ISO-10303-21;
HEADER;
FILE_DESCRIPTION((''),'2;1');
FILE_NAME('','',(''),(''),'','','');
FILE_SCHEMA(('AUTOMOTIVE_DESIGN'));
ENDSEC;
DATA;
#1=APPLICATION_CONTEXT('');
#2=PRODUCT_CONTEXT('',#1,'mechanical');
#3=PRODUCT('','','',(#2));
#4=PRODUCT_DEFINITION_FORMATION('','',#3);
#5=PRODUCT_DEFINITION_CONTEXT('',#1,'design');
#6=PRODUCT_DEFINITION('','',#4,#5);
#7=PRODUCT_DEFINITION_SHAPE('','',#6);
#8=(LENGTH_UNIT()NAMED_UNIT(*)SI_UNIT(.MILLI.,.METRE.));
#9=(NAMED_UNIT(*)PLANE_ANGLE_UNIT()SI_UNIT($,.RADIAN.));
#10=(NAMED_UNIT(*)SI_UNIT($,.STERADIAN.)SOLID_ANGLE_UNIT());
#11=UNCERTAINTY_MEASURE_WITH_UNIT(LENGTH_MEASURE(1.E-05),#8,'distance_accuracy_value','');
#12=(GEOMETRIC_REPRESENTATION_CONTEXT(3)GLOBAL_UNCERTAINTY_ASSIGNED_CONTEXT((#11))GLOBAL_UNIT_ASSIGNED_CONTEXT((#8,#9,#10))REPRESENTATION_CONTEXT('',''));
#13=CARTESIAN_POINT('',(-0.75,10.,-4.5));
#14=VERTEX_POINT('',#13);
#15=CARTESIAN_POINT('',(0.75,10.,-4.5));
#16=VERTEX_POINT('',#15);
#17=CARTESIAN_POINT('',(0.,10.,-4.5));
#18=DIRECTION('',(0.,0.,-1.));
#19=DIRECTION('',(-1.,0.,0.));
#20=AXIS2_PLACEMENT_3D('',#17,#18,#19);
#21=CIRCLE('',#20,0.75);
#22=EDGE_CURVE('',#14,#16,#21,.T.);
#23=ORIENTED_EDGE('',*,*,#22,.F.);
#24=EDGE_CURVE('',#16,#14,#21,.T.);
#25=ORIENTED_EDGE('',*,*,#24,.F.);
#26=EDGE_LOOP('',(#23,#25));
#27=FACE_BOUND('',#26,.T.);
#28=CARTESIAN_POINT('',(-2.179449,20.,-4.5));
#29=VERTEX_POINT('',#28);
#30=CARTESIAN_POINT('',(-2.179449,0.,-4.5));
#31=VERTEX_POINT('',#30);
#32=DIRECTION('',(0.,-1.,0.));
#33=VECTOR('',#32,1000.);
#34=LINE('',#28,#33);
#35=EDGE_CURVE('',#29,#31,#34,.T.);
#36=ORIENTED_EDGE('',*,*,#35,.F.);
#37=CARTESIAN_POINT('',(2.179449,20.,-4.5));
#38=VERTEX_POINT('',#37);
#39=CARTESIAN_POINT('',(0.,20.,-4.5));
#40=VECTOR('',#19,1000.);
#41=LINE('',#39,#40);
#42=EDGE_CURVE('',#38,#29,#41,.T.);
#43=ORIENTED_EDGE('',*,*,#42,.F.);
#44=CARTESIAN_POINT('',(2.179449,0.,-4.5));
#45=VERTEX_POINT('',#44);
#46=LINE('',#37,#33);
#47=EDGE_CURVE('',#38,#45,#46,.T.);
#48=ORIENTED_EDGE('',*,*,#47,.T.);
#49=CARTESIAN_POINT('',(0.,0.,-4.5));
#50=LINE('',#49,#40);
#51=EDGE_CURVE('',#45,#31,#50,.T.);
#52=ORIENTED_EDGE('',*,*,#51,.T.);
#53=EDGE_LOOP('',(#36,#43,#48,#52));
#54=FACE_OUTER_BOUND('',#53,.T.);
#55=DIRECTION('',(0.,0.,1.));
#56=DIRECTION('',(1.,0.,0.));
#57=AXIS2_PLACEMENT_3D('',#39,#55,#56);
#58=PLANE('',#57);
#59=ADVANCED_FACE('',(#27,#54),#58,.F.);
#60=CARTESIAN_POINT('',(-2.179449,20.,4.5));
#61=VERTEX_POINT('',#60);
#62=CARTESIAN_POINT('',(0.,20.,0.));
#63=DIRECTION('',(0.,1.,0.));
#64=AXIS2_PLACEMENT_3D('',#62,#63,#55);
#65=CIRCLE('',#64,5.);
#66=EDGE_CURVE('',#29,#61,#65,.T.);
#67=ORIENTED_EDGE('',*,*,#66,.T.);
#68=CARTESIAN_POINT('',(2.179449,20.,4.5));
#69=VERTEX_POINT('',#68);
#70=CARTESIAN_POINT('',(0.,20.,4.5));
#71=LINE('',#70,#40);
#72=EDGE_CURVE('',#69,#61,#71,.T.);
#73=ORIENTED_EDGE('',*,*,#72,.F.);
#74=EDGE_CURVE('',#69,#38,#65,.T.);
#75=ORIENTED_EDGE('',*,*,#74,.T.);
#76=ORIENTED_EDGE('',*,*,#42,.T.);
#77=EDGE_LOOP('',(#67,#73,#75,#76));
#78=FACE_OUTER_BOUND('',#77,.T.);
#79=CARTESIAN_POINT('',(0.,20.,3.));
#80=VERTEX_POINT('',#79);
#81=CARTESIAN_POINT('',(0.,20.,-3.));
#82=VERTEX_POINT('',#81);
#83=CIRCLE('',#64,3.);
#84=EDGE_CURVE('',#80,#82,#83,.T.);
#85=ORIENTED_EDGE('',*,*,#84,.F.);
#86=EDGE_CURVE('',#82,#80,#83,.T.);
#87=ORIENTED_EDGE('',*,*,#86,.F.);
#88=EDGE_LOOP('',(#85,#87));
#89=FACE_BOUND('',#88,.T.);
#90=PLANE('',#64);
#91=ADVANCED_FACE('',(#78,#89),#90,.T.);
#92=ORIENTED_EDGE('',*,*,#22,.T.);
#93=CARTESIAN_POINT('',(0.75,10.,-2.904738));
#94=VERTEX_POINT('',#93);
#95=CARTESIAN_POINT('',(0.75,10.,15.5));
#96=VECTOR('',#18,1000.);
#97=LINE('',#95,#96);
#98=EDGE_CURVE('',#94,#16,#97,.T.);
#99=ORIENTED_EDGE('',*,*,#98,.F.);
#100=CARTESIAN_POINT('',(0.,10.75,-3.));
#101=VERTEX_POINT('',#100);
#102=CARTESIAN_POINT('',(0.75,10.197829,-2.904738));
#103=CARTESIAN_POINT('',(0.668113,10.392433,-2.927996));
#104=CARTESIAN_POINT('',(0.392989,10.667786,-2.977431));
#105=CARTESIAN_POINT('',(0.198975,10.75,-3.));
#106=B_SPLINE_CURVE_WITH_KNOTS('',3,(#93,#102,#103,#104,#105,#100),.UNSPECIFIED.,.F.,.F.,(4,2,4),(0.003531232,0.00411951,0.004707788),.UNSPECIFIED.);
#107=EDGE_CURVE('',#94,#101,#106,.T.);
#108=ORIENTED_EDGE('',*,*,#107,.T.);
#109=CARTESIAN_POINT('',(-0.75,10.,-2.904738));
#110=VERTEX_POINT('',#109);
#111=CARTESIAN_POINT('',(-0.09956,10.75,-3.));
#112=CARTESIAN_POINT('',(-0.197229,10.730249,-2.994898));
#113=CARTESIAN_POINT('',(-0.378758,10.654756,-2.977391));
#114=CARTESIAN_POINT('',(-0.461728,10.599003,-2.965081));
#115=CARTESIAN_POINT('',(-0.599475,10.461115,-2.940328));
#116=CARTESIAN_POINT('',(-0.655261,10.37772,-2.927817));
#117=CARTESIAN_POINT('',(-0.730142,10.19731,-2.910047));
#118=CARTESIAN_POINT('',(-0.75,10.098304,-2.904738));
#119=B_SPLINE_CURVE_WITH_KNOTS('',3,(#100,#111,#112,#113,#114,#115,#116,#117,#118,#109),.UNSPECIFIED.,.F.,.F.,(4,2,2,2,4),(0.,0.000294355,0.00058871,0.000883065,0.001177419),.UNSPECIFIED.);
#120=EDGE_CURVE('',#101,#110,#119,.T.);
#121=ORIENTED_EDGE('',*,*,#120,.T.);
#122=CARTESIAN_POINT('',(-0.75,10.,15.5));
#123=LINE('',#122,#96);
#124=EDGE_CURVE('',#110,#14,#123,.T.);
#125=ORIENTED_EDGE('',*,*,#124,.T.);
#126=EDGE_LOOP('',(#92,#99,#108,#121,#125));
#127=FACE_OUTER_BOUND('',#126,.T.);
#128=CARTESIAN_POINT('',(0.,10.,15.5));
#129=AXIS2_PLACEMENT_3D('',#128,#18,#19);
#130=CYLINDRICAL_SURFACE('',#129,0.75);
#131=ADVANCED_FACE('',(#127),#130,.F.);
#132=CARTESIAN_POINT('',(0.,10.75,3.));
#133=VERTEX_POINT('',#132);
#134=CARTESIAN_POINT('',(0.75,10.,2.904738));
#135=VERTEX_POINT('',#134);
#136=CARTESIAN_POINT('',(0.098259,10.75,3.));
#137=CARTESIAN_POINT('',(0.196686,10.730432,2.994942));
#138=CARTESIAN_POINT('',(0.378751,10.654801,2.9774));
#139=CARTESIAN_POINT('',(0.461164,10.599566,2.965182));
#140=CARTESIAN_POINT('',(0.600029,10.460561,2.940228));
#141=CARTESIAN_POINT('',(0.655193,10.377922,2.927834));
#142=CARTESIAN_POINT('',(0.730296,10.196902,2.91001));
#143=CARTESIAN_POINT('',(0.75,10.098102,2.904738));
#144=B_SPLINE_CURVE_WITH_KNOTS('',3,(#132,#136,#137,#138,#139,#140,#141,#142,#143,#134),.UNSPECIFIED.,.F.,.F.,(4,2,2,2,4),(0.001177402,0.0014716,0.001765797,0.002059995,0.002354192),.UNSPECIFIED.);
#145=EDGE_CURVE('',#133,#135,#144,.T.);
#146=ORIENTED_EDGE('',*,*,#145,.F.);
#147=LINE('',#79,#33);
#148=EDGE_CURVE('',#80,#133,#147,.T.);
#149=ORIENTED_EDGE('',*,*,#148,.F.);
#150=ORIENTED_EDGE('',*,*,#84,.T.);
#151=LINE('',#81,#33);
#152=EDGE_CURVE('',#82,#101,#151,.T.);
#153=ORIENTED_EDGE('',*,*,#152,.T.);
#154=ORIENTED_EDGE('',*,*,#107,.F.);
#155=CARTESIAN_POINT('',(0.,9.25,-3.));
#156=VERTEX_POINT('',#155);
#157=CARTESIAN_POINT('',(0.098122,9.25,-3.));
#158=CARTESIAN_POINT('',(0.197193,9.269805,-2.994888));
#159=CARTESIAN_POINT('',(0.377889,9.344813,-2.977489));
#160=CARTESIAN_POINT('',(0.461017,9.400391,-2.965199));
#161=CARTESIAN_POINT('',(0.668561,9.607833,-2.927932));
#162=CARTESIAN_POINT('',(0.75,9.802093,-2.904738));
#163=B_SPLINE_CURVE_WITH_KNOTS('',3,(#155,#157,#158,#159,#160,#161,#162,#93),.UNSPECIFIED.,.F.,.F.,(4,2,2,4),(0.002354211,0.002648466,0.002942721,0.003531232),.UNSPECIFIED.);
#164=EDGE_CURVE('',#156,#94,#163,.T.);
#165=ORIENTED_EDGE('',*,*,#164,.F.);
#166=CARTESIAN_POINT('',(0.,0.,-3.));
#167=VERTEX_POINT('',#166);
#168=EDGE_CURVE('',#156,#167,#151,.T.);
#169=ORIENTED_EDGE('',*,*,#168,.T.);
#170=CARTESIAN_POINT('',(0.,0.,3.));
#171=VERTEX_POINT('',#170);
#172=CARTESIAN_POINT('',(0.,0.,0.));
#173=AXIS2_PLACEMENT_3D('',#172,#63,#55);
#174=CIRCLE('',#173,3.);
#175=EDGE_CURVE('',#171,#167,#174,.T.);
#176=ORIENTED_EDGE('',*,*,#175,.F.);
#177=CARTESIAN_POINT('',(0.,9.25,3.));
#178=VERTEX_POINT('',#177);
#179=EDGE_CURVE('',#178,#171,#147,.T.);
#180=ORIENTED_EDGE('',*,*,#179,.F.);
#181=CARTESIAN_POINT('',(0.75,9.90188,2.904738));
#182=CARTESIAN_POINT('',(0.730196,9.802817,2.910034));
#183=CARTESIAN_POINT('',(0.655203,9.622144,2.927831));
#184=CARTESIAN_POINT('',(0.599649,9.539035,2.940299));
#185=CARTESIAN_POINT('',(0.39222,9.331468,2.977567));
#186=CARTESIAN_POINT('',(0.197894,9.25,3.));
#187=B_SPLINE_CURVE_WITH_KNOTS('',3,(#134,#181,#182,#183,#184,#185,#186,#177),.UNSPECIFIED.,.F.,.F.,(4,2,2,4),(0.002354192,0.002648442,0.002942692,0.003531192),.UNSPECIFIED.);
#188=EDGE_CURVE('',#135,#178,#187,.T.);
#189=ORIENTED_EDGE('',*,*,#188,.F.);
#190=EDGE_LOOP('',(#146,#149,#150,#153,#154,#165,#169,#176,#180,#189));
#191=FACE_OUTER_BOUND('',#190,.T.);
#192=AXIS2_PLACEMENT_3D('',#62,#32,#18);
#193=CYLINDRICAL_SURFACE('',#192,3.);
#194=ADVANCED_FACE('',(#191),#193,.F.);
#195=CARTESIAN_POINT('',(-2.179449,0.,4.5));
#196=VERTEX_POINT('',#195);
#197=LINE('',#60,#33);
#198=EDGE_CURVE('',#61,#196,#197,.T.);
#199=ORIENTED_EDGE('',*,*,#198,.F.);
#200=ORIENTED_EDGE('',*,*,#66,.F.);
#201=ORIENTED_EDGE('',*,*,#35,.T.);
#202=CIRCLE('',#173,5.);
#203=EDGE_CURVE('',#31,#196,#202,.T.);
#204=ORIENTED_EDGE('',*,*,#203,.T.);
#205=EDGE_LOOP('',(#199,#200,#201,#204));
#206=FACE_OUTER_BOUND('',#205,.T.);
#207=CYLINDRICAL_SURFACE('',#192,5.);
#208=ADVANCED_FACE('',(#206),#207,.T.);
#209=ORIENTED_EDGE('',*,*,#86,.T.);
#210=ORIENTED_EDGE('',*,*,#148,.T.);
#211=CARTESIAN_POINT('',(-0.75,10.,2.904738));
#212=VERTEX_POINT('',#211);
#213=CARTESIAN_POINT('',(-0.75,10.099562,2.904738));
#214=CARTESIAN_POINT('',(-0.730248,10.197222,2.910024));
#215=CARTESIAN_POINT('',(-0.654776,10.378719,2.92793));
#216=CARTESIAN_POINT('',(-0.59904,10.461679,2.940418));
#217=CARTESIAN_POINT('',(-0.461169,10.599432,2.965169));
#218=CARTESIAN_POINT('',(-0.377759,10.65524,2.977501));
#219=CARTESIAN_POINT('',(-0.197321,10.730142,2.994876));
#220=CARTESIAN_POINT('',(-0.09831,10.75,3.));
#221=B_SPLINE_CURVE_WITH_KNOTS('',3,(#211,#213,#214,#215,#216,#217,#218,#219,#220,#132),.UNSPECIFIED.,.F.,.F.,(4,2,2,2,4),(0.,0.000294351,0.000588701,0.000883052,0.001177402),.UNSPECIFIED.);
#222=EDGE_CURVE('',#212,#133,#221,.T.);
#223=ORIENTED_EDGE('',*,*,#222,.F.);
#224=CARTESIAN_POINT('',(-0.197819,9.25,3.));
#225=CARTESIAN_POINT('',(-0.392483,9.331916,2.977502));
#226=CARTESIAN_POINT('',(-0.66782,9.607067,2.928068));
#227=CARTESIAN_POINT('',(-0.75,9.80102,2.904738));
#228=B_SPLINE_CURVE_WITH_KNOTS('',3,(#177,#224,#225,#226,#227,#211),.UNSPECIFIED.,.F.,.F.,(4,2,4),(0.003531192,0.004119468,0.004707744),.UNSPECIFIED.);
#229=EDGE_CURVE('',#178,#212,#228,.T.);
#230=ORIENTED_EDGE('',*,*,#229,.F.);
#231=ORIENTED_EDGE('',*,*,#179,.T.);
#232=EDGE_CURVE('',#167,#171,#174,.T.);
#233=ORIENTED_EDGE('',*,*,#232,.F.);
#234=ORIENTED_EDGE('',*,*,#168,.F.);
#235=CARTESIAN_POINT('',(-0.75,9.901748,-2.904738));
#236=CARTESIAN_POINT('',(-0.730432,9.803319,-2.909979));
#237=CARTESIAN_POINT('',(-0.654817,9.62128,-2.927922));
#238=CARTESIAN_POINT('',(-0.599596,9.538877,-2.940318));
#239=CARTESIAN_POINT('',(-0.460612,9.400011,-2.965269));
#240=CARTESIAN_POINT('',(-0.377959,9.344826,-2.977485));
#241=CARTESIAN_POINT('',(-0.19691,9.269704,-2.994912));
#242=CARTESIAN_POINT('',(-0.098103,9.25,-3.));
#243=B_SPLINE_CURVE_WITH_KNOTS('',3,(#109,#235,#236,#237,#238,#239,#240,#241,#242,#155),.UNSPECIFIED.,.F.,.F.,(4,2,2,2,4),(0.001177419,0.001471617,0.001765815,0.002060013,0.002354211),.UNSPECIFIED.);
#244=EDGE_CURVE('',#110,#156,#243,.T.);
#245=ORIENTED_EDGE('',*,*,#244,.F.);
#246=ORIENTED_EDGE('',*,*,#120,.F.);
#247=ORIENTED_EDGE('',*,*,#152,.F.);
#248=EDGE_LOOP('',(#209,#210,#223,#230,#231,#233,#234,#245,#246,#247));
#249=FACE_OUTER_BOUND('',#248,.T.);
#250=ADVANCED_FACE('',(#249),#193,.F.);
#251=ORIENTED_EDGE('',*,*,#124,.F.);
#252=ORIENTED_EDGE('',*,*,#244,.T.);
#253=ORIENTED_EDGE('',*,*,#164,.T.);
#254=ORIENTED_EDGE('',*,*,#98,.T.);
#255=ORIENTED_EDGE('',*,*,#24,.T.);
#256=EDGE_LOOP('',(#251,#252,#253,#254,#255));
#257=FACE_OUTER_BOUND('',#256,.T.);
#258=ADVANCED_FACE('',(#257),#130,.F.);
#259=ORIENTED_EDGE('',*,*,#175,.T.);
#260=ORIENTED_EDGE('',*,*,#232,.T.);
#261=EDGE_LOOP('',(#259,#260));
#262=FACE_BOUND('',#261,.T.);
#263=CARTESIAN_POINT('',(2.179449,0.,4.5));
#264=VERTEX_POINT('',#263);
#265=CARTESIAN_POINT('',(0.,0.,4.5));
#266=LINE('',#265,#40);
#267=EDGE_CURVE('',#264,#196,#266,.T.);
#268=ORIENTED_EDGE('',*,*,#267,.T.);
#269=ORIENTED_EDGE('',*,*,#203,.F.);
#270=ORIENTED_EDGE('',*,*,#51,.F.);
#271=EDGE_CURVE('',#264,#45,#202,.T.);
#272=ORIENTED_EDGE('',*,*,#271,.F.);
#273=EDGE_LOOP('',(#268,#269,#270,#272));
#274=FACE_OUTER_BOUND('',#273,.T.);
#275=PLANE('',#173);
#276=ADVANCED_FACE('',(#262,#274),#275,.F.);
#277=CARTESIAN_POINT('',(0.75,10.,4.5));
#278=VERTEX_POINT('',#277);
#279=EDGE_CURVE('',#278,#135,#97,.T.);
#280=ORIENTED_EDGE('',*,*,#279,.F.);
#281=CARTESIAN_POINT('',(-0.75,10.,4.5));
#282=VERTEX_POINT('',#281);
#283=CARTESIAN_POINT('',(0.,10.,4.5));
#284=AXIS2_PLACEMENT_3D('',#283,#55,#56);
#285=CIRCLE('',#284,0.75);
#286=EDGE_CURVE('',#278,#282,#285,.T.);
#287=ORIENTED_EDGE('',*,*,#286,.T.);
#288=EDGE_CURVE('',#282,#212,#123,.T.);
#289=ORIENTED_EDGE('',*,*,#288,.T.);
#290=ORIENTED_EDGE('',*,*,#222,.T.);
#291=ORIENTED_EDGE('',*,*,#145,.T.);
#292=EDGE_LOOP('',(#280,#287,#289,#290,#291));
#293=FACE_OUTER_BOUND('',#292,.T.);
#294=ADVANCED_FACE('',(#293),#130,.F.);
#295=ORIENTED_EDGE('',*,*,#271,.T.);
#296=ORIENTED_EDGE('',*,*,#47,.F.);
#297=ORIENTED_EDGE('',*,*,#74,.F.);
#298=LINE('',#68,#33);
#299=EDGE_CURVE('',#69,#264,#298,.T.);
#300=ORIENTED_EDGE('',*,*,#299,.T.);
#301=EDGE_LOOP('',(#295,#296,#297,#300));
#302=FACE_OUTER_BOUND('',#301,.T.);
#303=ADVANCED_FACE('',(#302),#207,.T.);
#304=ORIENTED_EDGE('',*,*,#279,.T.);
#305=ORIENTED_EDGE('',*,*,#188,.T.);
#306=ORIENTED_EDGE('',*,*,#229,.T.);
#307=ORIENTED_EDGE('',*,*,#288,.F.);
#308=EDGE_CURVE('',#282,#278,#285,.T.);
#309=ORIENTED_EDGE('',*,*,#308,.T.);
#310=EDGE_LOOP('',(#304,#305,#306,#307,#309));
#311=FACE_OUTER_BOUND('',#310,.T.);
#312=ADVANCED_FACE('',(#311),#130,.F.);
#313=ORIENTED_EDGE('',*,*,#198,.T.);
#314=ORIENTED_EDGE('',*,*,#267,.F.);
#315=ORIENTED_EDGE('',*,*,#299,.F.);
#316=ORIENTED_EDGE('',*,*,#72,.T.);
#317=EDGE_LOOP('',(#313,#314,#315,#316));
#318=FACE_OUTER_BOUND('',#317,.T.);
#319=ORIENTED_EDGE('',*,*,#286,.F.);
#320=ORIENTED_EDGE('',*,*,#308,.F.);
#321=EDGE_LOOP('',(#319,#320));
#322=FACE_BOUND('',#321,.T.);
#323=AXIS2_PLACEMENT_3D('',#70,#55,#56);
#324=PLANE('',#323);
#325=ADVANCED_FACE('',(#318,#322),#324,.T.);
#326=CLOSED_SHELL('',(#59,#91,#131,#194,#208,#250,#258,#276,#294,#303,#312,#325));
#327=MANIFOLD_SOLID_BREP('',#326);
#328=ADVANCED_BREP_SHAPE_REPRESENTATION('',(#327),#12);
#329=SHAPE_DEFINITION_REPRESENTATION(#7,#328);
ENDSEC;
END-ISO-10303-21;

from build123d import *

# Parameters (mm, degrees)
SKETCH1_R           = 3
BOSS_EXTRUDE1_DEPTH = 20
SKETCH2_R           = 0.75
CUT_EXTRUDE1_DEPTH  = 20


with BuildPart() as part:
    # Sketch1 → Boss-Extrude1 (new body)
    with BuildSketch(Plane(origin=(0, 0, 0), x_dir=(1, 0, 0), z_dir=(0, 1, 0))):
        with BuildLine():
            Line((2.179449472, -4.5), (-2.179449472, -4.5))
            ThreePointArc((-2.179449472, -4.5), (-5, 0), (-2.179449472, 4.5))
            Line((-2.179449472, 4.5), (2.179449472, 4.5))
            ThreePointArc((2.179449472, 4.5), (5, 0), (2.179449472, -4.5))
        make_face()
        with Locations(Location((0, 0, 0), (0, 0, 270))):
            Circle(SKETCH1_R, mode=Mode.SUBTRACT)
    extrude(amount=BOSS_EXTRUDE1_DEPTH)

    # Sketch2 → Cut-Extrude1 (cut)
    with BuildSketch(Plane(origin=(0, 0, -4.5), x_dir=(-1, 0, 0), z_dir=(0, 0, -1))):
        with Locations((0, 10)):
            Circle(SKETCH2_R)
    extrude(amount=-CUT_EXTRUDE1_DEPTH, mode=Mode.SUBTRACT)


solid = part.part
